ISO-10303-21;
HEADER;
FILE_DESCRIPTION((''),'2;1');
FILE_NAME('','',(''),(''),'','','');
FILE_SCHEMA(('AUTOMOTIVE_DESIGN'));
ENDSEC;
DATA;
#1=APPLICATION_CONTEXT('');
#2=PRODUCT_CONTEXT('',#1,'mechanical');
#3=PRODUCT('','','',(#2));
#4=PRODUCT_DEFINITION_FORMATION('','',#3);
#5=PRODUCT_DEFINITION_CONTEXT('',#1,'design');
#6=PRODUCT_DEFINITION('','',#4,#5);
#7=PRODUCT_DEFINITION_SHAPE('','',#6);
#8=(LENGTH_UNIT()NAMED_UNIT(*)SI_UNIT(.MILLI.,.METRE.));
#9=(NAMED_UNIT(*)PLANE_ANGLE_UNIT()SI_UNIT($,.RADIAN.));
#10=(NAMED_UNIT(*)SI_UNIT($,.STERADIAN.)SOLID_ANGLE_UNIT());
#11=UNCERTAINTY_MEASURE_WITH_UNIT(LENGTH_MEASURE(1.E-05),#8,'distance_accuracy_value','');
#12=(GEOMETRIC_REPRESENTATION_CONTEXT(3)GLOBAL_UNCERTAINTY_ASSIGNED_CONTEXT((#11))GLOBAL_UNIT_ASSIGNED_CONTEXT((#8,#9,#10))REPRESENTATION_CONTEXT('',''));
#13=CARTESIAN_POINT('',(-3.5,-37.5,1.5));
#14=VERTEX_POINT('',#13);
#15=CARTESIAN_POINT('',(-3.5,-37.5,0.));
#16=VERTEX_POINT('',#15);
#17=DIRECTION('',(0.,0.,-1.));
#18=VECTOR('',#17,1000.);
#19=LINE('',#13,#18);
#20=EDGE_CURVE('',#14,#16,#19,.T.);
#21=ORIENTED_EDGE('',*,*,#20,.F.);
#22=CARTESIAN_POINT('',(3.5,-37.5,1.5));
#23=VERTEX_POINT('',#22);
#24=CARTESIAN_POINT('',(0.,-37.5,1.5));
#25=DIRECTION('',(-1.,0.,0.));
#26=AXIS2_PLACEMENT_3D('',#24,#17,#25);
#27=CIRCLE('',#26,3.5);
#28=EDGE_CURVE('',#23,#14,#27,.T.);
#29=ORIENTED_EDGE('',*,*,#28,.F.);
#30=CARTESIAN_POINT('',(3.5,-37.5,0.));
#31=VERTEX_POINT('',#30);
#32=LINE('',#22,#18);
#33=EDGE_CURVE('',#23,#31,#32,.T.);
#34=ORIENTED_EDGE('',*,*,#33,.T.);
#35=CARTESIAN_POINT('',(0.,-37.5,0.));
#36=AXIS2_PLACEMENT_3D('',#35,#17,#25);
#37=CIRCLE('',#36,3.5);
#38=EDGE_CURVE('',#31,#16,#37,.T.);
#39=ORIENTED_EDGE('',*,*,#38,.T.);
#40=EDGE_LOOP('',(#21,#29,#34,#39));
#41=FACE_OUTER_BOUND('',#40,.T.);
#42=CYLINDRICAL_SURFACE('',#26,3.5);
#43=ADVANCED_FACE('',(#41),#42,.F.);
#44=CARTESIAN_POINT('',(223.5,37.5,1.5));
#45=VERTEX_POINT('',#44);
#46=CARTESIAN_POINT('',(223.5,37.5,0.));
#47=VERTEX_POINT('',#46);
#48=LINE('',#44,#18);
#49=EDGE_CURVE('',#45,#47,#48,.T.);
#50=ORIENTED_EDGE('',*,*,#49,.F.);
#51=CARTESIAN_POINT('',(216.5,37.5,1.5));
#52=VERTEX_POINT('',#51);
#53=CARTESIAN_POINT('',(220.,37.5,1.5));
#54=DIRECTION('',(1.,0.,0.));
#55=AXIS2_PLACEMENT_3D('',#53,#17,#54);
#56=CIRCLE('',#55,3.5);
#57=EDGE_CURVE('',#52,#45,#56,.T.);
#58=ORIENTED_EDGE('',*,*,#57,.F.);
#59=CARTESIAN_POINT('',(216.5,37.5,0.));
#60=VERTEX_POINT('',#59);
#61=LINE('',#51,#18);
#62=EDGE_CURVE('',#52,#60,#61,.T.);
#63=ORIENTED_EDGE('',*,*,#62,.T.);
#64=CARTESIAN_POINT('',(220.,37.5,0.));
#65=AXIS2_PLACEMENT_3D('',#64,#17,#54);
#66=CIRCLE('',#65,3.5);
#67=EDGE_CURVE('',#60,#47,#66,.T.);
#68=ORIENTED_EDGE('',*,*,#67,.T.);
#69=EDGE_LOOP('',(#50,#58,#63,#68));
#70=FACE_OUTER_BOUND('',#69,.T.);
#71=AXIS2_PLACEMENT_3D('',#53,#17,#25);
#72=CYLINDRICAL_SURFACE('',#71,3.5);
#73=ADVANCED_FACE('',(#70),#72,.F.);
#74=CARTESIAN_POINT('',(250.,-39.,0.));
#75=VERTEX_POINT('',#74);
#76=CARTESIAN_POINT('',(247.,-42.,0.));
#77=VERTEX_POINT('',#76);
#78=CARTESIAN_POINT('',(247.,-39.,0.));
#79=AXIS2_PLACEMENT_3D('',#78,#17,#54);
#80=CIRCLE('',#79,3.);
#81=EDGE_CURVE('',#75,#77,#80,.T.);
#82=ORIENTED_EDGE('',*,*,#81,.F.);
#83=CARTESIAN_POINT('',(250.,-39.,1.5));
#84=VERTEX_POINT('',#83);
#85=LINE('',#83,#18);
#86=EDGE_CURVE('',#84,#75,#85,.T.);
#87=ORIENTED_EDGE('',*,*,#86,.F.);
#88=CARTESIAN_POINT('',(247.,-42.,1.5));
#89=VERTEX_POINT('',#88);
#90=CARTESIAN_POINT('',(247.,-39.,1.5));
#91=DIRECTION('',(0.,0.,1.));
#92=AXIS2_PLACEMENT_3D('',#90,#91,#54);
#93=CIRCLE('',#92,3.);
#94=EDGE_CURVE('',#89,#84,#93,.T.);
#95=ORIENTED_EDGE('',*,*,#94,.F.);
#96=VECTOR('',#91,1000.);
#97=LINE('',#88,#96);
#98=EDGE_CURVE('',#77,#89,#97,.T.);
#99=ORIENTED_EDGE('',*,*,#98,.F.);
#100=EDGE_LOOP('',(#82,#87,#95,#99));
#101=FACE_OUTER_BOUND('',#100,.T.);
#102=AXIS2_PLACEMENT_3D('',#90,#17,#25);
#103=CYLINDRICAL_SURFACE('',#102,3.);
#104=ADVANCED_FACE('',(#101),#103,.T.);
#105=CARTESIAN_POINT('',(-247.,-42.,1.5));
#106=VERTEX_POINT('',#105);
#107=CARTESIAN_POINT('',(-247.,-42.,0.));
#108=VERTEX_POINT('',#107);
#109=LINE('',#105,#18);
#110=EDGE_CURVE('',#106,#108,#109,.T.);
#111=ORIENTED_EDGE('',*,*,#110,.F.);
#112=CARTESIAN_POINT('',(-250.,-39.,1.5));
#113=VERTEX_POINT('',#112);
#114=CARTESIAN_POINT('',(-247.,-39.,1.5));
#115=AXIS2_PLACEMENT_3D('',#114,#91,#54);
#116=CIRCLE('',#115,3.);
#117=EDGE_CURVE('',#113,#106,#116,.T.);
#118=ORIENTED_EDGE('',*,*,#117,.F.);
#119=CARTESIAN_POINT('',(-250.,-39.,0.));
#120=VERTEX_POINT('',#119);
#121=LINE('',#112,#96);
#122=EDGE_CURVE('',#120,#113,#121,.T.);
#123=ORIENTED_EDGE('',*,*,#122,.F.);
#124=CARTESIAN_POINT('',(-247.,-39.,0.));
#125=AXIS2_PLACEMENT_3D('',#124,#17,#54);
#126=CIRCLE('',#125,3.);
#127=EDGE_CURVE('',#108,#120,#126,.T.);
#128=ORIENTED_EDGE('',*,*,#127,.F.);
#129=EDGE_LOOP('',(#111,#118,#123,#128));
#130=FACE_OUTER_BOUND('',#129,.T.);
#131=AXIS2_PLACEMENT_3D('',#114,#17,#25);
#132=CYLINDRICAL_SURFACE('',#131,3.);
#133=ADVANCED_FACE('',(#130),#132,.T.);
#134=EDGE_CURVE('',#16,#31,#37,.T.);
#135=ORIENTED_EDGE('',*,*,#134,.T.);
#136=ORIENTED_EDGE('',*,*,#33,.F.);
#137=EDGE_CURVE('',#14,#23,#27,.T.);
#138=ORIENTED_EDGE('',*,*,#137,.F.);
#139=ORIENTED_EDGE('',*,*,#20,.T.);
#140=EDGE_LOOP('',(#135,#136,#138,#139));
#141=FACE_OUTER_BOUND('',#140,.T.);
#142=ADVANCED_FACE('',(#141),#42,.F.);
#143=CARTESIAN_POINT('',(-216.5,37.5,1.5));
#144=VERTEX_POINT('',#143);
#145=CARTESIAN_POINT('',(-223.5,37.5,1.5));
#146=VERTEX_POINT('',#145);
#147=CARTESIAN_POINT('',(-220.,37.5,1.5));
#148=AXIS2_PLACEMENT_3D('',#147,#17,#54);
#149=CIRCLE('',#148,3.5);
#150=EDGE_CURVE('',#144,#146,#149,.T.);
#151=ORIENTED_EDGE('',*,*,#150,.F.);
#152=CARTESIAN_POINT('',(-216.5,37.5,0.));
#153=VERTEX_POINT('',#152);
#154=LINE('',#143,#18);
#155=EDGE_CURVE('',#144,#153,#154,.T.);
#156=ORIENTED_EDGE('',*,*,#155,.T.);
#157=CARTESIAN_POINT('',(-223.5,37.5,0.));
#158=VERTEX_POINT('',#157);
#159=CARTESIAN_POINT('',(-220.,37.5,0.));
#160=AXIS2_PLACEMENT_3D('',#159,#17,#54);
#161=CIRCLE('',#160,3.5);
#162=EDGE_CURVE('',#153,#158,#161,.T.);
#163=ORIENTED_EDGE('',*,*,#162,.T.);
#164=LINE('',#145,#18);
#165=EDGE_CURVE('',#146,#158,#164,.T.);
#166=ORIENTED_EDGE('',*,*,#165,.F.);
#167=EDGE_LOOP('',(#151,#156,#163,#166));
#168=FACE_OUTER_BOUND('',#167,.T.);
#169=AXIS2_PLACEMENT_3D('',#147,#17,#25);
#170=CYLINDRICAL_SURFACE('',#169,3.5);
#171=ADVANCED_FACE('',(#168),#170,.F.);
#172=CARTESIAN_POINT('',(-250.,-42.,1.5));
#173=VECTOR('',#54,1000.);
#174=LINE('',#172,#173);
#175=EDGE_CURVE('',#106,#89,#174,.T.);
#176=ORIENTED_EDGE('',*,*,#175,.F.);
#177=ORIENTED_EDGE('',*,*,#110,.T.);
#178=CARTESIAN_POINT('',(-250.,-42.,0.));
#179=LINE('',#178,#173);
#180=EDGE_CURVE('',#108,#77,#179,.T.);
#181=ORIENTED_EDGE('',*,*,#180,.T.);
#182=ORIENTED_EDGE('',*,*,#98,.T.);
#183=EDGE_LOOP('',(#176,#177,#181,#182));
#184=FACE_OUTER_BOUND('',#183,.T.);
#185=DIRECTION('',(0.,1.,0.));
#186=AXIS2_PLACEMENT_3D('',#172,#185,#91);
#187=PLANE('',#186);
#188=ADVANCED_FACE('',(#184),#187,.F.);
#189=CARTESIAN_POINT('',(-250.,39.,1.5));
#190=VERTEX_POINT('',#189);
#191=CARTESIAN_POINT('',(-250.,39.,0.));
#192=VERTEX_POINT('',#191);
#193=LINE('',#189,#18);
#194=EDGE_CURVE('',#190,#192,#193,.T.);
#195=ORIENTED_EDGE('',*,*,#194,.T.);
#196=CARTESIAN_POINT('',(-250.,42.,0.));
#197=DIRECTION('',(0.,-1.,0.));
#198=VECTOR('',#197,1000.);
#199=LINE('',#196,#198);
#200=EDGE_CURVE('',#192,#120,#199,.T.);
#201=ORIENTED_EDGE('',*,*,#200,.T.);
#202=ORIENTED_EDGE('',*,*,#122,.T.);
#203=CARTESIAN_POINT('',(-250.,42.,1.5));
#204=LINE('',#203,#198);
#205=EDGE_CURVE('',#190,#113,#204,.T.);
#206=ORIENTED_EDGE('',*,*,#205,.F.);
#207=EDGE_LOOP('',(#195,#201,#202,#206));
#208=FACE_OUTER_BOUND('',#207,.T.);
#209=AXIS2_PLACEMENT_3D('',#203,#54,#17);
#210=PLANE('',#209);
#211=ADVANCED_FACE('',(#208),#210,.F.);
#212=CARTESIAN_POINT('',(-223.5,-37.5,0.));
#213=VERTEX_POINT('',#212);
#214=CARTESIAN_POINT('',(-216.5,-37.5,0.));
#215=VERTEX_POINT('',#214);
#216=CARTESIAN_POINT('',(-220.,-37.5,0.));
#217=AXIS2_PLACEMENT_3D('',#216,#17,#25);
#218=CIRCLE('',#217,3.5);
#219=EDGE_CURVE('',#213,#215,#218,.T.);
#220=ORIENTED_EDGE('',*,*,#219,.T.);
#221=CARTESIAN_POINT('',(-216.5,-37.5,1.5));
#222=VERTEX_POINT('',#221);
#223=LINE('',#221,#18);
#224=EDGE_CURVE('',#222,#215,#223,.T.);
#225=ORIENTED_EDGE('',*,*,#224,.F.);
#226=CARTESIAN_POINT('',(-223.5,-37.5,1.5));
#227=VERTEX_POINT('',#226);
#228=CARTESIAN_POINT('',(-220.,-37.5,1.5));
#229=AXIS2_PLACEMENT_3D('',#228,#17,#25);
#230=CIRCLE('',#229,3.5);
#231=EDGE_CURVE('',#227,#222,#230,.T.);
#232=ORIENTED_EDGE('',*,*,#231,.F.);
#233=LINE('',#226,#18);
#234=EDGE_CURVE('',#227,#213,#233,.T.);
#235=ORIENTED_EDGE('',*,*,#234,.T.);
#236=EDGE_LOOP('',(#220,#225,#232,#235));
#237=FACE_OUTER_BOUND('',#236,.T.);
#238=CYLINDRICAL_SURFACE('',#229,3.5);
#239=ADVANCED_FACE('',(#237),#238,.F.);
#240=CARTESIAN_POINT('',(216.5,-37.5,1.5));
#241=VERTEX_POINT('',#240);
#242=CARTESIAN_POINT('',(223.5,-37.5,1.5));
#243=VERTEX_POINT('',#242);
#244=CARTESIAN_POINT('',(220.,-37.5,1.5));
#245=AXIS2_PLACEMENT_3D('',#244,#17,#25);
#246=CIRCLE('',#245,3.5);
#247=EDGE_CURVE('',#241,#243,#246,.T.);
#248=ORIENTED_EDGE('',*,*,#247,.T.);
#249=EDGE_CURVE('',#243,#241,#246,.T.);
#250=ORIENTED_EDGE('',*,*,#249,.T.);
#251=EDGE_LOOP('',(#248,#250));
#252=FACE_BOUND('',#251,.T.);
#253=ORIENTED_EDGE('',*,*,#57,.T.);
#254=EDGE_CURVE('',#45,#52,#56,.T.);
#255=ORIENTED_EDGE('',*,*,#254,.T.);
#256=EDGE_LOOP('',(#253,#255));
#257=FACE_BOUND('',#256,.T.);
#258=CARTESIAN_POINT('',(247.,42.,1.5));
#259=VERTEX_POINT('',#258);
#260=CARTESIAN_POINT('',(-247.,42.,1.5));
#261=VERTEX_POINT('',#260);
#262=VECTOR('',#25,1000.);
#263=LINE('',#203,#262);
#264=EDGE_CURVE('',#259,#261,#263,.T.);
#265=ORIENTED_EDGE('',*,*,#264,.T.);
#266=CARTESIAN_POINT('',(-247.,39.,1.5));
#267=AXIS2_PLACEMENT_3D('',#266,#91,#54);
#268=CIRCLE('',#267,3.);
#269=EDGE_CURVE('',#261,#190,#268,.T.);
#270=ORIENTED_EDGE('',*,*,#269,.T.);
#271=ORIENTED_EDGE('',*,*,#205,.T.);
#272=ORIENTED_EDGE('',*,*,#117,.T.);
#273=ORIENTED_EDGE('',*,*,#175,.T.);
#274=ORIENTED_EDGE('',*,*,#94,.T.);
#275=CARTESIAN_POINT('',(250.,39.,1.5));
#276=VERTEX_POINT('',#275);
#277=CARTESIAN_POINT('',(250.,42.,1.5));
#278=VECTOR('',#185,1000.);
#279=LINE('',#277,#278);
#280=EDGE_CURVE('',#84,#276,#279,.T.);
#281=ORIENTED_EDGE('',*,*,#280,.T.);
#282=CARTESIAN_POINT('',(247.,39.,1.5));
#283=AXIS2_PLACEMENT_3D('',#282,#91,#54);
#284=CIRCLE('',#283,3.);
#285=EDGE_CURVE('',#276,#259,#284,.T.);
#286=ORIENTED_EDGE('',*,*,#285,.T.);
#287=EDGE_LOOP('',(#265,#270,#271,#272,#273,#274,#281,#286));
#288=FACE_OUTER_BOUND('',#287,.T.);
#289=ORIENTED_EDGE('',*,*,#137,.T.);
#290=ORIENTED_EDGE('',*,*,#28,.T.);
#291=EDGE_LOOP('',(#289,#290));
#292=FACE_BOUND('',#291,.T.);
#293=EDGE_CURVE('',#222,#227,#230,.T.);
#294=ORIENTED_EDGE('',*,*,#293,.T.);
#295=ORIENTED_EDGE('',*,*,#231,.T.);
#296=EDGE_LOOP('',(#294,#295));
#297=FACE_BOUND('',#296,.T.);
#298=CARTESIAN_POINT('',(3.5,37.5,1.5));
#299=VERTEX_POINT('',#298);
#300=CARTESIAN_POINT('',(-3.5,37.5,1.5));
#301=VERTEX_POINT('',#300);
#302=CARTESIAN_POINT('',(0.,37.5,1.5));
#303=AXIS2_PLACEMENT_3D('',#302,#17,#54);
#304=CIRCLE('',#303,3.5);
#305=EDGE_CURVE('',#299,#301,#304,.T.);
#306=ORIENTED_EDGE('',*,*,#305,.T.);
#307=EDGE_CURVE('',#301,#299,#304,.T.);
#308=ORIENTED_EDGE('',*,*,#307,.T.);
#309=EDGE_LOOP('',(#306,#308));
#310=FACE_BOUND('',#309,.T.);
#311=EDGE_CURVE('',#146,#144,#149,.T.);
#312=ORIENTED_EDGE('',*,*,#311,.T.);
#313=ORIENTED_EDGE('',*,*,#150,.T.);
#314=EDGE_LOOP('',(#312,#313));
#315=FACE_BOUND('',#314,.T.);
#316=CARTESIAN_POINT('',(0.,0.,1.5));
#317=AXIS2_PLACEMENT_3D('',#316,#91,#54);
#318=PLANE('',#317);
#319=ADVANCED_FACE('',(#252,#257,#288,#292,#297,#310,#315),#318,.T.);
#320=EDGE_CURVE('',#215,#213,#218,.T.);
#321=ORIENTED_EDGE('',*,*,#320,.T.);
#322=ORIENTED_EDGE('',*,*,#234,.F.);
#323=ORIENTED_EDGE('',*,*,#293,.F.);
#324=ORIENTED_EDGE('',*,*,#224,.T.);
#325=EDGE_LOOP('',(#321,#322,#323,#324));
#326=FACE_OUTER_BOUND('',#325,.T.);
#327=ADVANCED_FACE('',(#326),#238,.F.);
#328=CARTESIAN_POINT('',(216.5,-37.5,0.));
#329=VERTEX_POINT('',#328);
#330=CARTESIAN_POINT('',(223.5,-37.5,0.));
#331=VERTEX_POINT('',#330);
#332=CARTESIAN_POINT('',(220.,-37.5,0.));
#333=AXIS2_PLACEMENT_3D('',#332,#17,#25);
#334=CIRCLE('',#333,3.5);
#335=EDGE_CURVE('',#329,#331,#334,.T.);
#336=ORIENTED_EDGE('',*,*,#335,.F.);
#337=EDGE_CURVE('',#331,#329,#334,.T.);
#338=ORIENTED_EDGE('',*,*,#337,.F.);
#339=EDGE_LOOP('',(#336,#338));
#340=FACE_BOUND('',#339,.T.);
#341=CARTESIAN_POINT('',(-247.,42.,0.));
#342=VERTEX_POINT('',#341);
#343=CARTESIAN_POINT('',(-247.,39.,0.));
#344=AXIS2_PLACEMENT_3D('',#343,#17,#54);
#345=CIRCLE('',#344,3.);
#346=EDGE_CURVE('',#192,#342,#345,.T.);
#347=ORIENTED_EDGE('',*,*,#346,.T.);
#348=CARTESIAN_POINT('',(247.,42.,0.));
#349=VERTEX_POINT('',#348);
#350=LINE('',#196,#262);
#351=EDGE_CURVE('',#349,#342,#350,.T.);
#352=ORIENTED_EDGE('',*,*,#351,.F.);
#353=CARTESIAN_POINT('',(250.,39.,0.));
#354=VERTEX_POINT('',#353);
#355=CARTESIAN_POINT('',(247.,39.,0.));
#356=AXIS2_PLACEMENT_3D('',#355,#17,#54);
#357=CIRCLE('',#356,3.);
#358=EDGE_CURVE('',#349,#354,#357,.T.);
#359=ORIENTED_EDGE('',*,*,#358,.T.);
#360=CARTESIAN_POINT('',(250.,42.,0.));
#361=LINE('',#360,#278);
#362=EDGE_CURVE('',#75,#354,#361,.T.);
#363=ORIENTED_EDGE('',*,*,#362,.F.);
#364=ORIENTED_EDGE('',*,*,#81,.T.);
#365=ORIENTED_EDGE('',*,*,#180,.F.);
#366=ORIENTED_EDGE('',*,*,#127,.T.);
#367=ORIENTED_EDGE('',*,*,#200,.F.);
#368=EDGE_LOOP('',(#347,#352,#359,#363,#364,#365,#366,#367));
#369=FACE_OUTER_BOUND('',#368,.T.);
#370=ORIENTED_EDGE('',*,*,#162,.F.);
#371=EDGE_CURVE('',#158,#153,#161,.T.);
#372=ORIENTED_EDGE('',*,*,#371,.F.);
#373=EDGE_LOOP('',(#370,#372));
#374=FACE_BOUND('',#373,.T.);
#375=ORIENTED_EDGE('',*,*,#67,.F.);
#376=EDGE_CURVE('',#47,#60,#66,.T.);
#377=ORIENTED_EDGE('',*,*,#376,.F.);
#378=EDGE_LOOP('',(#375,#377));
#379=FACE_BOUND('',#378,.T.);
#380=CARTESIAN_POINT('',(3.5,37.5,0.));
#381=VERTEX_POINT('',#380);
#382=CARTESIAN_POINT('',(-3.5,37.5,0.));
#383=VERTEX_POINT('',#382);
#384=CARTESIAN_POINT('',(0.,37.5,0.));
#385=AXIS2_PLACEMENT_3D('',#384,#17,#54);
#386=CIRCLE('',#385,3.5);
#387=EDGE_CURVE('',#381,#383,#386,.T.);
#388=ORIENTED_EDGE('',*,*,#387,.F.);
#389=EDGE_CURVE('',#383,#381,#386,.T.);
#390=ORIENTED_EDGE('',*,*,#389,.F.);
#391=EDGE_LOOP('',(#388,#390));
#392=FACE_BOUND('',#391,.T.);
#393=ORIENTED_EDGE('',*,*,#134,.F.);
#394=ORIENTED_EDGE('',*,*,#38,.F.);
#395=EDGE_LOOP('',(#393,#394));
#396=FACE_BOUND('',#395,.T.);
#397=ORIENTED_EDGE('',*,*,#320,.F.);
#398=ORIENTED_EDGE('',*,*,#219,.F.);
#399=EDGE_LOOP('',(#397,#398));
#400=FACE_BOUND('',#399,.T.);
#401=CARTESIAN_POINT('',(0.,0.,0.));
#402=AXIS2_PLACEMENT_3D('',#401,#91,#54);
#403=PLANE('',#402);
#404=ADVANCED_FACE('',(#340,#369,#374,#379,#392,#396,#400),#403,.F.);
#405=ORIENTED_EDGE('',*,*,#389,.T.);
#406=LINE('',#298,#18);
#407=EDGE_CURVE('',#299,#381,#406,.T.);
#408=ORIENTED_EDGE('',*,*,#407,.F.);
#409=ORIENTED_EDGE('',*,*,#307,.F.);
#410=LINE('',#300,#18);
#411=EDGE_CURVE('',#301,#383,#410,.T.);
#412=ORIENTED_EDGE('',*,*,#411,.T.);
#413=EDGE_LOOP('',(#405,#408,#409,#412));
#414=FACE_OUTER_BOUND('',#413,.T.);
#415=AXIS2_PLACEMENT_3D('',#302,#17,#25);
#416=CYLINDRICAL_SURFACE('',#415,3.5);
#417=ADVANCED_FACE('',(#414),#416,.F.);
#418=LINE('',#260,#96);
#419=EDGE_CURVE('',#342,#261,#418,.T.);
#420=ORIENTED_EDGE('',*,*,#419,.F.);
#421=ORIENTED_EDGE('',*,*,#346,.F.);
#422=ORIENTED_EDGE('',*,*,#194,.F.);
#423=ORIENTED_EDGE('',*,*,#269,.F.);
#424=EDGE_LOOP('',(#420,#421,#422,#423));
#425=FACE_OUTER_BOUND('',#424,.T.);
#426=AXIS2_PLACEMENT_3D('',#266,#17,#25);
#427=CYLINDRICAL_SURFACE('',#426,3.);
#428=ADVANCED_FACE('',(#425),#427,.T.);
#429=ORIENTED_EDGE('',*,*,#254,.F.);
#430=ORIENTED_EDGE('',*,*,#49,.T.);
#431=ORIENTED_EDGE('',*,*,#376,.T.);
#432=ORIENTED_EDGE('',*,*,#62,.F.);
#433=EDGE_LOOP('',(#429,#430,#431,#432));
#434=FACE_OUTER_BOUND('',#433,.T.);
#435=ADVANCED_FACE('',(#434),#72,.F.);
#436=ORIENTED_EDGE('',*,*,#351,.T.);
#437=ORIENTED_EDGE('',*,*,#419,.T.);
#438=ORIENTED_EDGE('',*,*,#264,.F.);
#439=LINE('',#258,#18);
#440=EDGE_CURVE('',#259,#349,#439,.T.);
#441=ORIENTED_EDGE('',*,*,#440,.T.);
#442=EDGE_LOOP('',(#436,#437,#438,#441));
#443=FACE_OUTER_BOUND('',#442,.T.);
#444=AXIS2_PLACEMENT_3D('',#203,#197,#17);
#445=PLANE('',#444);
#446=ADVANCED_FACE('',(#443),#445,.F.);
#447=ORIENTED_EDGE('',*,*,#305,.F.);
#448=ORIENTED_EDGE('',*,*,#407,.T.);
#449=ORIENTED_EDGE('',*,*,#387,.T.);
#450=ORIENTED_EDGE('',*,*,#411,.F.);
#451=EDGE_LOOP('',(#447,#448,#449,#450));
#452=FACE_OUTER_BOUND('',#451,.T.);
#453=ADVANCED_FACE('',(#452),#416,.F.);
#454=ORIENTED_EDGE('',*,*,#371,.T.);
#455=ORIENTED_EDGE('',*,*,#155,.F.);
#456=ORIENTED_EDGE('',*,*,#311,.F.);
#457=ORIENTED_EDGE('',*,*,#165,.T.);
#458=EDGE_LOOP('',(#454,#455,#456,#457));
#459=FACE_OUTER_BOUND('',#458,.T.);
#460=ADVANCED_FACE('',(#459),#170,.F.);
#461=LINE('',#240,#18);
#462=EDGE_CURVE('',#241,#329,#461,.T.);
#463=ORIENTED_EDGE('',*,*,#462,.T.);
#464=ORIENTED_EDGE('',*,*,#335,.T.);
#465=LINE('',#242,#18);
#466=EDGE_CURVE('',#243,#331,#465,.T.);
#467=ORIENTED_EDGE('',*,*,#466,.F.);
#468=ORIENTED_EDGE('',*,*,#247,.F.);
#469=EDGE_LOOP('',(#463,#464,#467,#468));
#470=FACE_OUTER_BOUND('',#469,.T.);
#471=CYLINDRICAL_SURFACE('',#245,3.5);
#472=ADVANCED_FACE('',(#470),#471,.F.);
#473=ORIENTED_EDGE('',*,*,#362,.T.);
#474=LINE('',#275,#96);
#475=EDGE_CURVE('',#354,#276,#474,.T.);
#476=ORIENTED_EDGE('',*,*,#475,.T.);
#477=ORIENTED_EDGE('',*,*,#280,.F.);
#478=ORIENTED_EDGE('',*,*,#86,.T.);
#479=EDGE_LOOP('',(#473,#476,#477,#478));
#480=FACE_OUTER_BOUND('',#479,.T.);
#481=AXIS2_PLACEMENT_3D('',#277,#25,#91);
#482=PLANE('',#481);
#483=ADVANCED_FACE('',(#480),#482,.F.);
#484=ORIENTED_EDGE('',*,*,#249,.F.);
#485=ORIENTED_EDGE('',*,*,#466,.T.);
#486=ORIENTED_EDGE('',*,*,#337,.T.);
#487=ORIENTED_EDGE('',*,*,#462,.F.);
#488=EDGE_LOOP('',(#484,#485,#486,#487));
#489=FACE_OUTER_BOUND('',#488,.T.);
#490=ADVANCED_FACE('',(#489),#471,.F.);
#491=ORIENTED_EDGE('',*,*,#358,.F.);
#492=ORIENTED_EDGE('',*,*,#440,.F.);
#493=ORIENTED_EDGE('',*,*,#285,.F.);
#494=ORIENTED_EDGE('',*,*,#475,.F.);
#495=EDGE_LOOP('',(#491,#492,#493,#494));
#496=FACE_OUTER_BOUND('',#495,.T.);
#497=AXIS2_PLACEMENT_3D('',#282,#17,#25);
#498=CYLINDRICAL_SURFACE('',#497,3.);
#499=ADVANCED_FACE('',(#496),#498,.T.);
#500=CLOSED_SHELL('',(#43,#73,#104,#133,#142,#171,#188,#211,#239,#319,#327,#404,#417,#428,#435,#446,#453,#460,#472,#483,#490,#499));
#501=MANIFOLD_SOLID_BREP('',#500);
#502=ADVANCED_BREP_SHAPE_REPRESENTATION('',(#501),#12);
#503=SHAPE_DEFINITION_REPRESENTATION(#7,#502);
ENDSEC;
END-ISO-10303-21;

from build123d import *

# Parameters (mm, degrees)
SKETCH_1_W          = 500
SKETCH_1_H          = 84
EXTRUDE_1_DEPTH     = 1.5
SKETCH_2_R          = 3.5
CUT_EXTRUDE_1_DEPTH = 254.507889424
FILLET_1_R          = 3


with BuildPart() as part:
    # 草图1 → 凸台-拉伸1 (new body)
    with BuildSketch(Plane.XY):
        Rectangle(SKETCH_1_W, SKETCH_1_H)
    extrude(amount=EXTRUDE_1_DEPTH)

    # 草图2 → 切除-拉伸1 (cut, through all)
    with BuildSketch(Plane(origin=(0, 0, 0), x_dir=(-1, 0, 0), z_dir=(0, 0, -1))):
        with Locations(Location((0, 37.5, 0), (0, 0, 180))):
            Circle(SKETCH_2_R)
        with Locations(Location((220, 37.5, 0), (0, 0, 180))):
            Circle(SKETCH_2_R)
        with Locations((-220, -37.5)):
            Circle(SKETCH_2_R)
        with Locations((220, -37.5)):
            Circle(SKETCH_2_R)
        with Locations((0, -37.5)):
            Circle(SKETCH_2_R)
        with Locations(Location((-220, 37.5, 0), (0, 0, 180))):
            Circle(SKETCH_2_R)
    extrude(amount=-CUT_EXTRUDE_1_DEPTH, mode=Mode.SUBTRACT)

    # 圆角1
    fillet_1_edges = [part.edges().sort_by_distance(p)[0] for p in [
        (250, -42, 0.75),
        (-250, -42, 0.75),
        (-250, 42, 0.75),
        (250, 42, 0.75),
    ]]
    fillet(fillet_1_edges, radius=FILLET_1_R)


solid = part.part
